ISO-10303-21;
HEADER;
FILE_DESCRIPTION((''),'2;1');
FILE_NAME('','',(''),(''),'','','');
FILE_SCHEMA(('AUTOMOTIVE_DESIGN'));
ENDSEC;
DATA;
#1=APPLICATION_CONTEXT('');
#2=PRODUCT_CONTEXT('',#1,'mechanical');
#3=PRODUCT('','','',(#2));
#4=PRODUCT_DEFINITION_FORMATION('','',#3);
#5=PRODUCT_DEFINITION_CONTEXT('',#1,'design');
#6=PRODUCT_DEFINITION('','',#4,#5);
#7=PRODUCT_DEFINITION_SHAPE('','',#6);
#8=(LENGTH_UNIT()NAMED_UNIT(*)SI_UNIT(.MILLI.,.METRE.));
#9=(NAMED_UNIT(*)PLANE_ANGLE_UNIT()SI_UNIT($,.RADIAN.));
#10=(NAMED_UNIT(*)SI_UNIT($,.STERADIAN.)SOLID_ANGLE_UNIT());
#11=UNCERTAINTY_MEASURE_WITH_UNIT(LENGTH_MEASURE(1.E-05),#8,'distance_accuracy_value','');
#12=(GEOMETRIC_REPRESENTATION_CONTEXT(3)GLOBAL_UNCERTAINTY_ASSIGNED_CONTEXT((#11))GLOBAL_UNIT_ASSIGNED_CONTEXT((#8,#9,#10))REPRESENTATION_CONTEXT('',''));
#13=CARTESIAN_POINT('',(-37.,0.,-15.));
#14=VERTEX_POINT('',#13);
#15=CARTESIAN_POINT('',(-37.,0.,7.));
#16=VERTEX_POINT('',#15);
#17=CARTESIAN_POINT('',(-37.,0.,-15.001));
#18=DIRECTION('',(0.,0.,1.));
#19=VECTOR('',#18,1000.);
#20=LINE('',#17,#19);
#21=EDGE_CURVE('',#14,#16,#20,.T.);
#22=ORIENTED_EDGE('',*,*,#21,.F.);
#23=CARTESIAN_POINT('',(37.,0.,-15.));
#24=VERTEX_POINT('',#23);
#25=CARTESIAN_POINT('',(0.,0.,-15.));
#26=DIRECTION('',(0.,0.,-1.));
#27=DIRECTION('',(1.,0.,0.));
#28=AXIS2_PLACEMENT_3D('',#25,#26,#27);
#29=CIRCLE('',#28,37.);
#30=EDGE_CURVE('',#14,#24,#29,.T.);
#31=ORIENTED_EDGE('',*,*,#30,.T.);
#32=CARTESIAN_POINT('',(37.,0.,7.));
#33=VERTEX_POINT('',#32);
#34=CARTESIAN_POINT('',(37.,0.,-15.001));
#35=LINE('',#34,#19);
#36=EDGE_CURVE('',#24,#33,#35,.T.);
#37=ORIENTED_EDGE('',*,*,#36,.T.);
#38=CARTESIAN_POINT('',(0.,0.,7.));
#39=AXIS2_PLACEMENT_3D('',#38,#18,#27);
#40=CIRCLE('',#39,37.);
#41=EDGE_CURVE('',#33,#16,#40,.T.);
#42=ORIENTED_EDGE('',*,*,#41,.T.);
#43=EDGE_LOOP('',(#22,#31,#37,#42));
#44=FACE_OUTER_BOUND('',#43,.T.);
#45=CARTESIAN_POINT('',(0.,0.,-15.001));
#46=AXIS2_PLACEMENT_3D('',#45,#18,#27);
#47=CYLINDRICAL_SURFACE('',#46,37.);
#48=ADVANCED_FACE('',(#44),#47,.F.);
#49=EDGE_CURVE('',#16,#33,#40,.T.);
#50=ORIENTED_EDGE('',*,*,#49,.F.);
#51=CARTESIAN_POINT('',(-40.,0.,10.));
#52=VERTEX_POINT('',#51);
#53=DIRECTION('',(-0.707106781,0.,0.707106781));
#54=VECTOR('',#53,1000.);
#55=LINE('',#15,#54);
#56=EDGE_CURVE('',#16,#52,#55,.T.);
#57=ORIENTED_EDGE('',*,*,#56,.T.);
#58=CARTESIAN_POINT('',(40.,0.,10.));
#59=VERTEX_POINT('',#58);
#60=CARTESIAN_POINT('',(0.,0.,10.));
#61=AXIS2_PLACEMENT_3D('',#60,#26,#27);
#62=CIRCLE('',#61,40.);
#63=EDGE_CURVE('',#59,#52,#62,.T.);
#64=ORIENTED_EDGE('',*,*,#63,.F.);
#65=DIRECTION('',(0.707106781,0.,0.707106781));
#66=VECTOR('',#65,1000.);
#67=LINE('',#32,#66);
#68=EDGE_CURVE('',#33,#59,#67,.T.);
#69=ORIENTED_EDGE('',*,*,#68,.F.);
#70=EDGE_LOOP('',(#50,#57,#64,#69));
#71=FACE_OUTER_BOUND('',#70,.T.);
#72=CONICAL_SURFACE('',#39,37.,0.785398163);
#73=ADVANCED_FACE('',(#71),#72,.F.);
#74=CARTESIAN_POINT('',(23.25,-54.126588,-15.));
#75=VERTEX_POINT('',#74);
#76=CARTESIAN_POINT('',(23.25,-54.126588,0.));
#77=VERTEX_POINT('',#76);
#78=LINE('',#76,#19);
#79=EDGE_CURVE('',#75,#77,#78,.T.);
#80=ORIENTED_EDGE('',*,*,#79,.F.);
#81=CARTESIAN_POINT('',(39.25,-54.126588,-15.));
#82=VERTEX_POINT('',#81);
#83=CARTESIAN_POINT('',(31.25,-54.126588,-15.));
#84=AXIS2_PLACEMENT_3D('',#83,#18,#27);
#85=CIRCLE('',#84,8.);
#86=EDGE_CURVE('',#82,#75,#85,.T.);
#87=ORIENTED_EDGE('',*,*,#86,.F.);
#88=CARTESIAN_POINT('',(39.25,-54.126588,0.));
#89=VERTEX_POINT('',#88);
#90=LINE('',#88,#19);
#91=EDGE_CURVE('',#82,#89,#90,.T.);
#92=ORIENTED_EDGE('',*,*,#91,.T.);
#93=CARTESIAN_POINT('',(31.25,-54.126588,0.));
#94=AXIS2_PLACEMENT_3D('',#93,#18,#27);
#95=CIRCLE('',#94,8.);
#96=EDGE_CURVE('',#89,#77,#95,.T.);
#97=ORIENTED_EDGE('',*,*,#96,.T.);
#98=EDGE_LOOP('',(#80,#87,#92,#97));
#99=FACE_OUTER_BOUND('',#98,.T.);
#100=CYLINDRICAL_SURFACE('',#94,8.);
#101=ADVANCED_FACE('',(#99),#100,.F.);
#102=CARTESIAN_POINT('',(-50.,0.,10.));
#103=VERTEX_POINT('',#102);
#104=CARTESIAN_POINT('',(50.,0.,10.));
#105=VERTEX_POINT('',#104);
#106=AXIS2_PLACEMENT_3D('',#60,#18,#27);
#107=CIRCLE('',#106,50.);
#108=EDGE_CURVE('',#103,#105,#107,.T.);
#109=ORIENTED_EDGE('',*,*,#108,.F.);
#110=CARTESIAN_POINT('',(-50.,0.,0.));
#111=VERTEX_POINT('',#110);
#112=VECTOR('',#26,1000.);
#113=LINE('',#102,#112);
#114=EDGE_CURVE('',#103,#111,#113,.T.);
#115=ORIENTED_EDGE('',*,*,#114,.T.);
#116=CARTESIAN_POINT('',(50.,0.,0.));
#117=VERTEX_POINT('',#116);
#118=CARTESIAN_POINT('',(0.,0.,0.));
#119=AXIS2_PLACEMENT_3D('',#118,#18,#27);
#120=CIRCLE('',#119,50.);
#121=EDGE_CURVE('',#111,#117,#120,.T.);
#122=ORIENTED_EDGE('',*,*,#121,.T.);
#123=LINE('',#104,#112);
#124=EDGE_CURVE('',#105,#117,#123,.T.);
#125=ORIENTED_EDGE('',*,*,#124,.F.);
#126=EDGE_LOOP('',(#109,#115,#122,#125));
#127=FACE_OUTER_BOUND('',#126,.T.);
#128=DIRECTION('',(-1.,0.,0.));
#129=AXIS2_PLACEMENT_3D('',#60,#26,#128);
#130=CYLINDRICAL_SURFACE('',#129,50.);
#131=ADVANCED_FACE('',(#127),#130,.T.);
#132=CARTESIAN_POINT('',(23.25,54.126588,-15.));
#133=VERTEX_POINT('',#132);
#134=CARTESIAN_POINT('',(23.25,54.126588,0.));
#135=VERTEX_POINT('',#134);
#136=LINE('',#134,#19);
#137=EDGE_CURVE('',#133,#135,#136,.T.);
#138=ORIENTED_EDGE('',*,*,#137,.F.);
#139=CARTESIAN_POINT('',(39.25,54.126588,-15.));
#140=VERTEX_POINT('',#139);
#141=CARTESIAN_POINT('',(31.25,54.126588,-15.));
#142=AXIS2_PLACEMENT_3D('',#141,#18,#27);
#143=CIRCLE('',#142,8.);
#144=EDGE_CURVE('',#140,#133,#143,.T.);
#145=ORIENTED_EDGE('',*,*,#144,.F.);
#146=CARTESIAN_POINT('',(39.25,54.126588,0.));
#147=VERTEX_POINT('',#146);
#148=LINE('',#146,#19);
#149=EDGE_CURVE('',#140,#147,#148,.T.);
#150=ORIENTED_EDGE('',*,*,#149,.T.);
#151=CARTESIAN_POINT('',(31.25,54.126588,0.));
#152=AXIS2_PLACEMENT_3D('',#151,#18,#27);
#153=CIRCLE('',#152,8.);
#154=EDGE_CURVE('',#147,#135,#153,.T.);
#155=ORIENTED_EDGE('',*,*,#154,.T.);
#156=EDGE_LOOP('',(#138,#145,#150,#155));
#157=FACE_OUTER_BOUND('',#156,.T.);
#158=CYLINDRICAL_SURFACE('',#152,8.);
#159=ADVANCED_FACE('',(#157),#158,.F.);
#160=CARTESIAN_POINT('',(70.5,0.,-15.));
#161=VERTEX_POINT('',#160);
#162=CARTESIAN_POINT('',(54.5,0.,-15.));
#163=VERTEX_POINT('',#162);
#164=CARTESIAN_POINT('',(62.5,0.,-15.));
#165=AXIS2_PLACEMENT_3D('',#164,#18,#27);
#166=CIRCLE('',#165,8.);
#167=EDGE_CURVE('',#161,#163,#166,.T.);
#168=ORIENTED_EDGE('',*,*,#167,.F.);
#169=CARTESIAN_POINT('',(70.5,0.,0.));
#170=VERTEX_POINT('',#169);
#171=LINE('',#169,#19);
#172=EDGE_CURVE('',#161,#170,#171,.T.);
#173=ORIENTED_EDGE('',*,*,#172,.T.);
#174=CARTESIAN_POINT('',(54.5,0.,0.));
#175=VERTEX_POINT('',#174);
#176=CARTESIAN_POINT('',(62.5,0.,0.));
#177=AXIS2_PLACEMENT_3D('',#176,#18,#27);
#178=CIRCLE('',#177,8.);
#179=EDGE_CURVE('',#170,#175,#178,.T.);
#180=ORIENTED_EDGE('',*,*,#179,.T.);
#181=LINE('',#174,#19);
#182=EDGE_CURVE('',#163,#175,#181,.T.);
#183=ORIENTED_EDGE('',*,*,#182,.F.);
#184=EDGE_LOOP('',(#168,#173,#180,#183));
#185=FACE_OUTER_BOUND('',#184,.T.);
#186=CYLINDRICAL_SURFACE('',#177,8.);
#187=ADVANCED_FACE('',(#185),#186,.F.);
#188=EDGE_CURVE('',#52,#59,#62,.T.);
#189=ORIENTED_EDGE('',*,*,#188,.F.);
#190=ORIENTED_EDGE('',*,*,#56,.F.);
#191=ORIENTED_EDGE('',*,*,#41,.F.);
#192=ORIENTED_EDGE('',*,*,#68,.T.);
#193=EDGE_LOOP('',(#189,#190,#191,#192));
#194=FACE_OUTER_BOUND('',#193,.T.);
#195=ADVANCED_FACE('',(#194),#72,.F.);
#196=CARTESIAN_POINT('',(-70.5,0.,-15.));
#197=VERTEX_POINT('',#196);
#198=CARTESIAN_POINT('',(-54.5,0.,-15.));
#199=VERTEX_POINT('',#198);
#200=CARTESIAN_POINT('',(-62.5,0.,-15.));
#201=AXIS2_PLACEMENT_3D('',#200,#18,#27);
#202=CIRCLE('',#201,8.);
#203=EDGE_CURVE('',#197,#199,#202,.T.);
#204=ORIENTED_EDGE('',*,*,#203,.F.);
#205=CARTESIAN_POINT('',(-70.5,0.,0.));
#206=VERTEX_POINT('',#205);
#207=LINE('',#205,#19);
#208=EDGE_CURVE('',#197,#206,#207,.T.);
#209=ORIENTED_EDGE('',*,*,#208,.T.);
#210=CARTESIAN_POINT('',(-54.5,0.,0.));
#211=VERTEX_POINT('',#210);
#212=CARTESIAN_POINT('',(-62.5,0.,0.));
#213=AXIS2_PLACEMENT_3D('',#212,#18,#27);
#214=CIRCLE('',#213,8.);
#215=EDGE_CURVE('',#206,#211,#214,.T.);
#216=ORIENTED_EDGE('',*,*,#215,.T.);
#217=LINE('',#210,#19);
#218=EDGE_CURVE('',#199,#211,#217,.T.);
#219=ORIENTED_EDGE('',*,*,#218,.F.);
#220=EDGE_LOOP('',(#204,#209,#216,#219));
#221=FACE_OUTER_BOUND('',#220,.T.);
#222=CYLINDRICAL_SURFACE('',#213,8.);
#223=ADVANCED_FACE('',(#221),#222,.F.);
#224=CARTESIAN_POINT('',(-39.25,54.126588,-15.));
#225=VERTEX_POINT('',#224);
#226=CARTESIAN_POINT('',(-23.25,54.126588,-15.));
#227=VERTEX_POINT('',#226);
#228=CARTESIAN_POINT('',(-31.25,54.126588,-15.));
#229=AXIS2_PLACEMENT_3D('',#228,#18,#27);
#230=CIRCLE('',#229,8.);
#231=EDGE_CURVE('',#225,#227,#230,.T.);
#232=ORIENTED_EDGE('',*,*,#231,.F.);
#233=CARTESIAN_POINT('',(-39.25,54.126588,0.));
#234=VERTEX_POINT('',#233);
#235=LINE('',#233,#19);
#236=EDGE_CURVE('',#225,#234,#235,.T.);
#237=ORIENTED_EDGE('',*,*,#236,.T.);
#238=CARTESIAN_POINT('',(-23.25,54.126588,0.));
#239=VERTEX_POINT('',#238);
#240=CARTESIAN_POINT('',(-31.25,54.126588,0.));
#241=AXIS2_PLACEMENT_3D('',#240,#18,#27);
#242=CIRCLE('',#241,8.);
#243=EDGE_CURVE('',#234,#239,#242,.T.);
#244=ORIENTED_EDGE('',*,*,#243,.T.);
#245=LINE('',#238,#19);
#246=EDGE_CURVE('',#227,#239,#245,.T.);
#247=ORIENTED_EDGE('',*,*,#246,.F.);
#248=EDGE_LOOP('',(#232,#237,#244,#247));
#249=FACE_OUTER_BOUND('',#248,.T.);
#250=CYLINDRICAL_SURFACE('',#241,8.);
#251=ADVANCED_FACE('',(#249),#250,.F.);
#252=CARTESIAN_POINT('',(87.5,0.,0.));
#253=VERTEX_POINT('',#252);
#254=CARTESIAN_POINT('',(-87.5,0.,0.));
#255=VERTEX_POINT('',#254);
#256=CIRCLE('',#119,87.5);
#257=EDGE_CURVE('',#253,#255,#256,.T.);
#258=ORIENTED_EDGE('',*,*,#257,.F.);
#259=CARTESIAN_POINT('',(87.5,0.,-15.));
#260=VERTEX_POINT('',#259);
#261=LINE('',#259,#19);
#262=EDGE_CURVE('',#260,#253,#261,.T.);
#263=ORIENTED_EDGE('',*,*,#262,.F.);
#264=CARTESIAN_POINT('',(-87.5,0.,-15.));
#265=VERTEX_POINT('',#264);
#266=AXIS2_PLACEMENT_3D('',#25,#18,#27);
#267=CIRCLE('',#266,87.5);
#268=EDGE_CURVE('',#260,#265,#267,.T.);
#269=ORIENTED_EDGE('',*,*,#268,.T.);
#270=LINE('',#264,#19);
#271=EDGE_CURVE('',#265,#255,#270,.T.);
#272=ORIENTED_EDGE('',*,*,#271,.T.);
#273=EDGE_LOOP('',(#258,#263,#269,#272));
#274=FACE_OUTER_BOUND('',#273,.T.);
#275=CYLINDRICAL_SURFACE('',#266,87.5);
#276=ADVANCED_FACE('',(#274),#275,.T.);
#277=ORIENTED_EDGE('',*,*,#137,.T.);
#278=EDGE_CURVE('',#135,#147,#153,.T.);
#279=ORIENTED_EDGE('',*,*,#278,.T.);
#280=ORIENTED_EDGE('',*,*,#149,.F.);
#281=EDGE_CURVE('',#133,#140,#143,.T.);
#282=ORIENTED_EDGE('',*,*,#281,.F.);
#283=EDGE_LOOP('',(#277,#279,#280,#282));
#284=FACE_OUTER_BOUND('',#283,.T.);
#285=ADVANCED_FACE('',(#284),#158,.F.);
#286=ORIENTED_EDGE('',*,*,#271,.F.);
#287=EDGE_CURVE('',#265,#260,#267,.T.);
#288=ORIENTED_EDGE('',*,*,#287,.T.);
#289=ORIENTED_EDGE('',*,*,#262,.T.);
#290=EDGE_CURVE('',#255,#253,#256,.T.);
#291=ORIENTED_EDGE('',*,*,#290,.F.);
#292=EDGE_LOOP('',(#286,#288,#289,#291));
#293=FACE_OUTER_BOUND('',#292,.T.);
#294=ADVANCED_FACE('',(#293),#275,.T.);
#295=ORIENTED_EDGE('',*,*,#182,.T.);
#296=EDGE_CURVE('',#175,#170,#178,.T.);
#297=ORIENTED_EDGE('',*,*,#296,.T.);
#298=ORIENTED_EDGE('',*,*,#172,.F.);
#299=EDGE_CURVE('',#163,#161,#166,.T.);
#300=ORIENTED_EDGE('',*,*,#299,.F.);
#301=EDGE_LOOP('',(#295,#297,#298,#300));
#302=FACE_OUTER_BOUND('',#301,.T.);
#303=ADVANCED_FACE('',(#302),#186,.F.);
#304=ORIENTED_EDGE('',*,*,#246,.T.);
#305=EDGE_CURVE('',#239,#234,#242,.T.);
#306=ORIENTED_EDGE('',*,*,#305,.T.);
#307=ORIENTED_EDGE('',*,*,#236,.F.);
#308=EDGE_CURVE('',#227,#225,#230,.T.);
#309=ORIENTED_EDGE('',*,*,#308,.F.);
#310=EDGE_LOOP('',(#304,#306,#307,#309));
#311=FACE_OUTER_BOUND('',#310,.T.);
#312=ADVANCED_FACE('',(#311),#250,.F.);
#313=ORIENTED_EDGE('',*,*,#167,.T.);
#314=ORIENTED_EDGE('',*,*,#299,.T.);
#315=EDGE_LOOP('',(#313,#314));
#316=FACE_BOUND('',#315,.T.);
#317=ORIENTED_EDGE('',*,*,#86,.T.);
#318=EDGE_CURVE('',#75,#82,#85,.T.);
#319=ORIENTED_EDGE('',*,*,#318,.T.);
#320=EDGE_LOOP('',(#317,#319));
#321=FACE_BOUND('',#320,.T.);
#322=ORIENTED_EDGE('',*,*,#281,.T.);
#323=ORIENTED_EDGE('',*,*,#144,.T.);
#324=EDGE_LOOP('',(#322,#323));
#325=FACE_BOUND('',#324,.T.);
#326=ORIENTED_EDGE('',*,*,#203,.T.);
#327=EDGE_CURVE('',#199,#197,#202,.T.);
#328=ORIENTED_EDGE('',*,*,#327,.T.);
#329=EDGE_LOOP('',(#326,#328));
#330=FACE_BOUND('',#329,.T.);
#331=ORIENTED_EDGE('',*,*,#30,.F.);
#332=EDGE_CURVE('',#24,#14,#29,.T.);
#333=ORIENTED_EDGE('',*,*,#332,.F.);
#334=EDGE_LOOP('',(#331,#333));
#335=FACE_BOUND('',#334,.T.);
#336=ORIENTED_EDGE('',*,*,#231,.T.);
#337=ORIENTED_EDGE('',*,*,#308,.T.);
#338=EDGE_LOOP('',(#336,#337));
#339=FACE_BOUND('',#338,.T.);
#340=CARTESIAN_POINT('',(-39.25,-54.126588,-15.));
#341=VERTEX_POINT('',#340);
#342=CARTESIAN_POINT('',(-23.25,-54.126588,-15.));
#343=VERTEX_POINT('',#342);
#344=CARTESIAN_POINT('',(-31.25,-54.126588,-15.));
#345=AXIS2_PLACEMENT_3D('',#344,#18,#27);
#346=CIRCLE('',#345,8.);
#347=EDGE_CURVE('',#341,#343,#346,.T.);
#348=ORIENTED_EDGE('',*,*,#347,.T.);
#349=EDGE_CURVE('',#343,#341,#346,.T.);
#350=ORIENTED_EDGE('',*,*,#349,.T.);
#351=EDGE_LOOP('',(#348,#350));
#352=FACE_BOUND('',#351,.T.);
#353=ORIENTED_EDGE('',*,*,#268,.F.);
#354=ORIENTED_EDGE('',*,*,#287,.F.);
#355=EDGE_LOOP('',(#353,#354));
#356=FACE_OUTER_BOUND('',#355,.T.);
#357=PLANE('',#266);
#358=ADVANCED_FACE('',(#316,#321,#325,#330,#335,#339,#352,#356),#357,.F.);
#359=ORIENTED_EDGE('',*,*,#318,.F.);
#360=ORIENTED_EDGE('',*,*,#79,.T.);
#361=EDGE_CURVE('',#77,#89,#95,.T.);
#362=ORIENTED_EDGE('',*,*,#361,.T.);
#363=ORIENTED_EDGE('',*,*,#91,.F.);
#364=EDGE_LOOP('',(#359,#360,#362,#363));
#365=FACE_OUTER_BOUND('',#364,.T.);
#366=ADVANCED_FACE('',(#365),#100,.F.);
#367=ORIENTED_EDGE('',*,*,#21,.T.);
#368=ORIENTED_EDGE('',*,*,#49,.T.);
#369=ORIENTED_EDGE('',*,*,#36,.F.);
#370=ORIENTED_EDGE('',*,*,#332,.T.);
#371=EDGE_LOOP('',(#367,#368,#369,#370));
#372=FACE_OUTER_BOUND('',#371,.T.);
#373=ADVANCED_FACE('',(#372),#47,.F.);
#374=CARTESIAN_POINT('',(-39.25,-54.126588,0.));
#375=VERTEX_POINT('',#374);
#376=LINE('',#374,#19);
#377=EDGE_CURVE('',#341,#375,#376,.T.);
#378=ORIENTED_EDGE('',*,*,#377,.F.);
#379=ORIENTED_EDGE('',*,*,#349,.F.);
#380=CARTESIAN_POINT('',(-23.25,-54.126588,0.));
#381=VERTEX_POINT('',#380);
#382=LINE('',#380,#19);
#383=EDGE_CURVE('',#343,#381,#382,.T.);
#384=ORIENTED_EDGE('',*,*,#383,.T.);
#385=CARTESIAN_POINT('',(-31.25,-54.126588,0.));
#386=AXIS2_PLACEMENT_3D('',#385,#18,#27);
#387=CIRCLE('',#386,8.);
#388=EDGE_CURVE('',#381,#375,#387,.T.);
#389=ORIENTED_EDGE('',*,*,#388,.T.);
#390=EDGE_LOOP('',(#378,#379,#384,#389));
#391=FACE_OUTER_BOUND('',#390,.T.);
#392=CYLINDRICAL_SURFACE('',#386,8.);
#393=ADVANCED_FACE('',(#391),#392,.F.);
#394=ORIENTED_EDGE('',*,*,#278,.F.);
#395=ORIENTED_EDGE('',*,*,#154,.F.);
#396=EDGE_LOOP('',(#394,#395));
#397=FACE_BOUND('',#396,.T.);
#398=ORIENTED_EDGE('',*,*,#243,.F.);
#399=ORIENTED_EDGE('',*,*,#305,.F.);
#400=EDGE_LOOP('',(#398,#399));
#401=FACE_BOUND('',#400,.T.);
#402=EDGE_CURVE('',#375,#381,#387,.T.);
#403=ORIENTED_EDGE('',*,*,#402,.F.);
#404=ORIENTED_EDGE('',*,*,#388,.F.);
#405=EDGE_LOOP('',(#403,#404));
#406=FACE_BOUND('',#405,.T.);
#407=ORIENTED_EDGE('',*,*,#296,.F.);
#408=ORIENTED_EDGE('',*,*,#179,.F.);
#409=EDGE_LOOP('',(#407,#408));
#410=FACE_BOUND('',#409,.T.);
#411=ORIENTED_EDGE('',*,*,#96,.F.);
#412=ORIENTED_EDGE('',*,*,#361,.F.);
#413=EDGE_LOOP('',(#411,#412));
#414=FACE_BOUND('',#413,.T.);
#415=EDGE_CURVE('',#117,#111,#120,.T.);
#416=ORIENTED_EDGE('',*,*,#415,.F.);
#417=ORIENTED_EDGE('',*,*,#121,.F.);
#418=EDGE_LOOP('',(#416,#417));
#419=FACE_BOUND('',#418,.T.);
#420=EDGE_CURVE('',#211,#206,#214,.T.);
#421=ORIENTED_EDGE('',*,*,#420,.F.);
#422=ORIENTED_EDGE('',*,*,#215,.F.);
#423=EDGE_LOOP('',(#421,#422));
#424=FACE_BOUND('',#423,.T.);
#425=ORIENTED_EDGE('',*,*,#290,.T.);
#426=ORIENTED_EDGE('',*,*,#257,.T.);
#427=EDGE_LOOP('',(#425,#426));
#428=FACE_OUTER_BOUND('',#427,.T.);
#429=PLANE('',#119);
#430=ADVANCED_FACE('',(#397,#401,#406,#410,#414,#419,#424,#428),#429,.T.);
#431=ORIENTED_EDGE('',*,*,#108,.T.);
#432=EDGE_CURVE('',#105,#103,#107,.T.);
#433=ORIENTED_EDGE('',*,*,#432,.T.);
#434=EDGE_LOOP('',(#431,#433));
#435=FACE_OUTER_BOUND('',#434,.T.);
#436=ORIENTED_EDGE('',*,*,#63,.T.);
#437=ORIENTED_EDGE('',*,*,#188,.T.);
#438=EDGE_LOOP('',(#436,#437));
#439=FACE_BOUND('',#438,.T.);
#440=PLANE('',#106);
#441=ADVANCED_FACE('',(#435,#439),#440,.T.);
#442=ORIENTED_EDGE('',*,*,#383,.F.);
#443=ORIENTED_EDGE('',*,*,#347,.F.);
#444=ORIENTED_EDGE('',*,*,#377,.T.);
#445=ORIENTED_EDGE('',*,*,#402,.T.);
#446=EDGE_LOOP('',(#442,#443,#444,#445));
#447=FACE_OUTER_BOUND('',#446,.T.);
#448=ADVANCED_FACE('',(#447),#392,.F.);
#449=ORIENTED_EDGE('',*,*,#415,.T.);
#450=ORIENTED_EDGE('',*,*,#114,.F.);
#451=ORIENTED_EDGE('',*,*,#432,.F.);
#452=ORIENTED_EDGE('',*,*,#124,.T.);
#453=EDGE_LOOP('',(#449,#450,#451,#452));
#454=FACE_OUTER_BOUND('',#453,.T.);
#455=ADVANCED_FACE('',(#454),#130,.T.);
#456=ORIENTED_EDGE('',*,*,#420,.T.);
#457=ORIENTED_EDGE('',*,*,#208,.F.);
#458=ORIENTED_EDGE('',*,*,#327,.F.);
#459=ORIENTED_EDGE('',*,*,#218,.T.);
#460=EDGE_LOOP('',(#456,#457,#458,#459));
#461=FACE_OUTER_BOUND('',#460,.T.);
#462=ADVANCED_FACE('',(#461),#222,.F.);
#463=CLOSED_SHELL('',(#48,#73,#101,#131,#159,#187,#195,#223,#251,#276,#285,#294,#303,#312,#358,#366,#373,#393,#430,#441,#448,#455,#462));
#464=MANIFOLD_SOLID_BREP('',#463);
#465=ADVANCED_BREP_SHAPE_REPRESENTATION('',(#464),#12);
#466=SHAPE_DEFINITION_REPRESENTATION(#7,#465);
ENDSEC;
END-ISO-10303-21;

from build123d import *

# Parameters (mm, degrees)
SKETCH1_R                  = 50
BOSS_EXTRUDE1_DEPTH        = 10
SKETCH2_R                  = 87.5
BOSS_EXTRUDE2_DEPTH        = 15
CUT_EXTRUDE1_REACH         = 128.244
SKETCH3_R                  = 37
F_16_0_16_DIAMETER_HOLE1_D = 16
CHAMFER1_SIZE              = 3


with BuildPart() as part:
    # Sketch1 → Boss-Extrude1 (new body)
    with BuildSketch(Plane.XY):
        Circle(SKETCH1_R)
    extrude(amount=BOSS_EXTRUDE1_DEPTH)

    # Sketch2 → Boss-Extrude2 (add)
    with BuildSketch(Plane.XY):
        Circle(SKETCH2_R)
    extrude(amount=-BOSS_EXTRUDE2_DEPTH)

    # Sketch3 → Cut-Extrude1 (cut, up to next)
    with BuildSketch(Plane.XY.offset(10), mode=Mode.PRIVATE) as cut_extrude1_sk1:
        Circle(SKETCH3_R)
    cut_extrude1_tool1 = extrude(cut_extrude1_sk1.sketch, amount=-CUT_EXTRUDE1_REACH, mode=Mode.PRIVATE) & part.part
    add(cut_extrude1_tool1.solids().sort_by_distance((0, 0, 10))[0], mode=Mode.SUBTRACT)

    # Ø16.0 (16) Diameter Hole1 (through all)
    with Locations(Plane.XY):
        with Locations((62.5, 0), (31.25, -54.126587737), (-31.25, -54.126587737), (-62.5, 0), (-31.25, 54.126587737), (31.25, 54.126587737)):
            Hole(F_16_0_16_DIAMETER_HOLE1_D / 2)

    # Chamfer1
    chamfer1_edges = [part.edges().sort_by_distance(p)[0] for p in [
        (-37, 0, 10),
    ]]
    chamfer(chamfer1_edges, length=CHAMFER1_SIZE)


solid = part.part
